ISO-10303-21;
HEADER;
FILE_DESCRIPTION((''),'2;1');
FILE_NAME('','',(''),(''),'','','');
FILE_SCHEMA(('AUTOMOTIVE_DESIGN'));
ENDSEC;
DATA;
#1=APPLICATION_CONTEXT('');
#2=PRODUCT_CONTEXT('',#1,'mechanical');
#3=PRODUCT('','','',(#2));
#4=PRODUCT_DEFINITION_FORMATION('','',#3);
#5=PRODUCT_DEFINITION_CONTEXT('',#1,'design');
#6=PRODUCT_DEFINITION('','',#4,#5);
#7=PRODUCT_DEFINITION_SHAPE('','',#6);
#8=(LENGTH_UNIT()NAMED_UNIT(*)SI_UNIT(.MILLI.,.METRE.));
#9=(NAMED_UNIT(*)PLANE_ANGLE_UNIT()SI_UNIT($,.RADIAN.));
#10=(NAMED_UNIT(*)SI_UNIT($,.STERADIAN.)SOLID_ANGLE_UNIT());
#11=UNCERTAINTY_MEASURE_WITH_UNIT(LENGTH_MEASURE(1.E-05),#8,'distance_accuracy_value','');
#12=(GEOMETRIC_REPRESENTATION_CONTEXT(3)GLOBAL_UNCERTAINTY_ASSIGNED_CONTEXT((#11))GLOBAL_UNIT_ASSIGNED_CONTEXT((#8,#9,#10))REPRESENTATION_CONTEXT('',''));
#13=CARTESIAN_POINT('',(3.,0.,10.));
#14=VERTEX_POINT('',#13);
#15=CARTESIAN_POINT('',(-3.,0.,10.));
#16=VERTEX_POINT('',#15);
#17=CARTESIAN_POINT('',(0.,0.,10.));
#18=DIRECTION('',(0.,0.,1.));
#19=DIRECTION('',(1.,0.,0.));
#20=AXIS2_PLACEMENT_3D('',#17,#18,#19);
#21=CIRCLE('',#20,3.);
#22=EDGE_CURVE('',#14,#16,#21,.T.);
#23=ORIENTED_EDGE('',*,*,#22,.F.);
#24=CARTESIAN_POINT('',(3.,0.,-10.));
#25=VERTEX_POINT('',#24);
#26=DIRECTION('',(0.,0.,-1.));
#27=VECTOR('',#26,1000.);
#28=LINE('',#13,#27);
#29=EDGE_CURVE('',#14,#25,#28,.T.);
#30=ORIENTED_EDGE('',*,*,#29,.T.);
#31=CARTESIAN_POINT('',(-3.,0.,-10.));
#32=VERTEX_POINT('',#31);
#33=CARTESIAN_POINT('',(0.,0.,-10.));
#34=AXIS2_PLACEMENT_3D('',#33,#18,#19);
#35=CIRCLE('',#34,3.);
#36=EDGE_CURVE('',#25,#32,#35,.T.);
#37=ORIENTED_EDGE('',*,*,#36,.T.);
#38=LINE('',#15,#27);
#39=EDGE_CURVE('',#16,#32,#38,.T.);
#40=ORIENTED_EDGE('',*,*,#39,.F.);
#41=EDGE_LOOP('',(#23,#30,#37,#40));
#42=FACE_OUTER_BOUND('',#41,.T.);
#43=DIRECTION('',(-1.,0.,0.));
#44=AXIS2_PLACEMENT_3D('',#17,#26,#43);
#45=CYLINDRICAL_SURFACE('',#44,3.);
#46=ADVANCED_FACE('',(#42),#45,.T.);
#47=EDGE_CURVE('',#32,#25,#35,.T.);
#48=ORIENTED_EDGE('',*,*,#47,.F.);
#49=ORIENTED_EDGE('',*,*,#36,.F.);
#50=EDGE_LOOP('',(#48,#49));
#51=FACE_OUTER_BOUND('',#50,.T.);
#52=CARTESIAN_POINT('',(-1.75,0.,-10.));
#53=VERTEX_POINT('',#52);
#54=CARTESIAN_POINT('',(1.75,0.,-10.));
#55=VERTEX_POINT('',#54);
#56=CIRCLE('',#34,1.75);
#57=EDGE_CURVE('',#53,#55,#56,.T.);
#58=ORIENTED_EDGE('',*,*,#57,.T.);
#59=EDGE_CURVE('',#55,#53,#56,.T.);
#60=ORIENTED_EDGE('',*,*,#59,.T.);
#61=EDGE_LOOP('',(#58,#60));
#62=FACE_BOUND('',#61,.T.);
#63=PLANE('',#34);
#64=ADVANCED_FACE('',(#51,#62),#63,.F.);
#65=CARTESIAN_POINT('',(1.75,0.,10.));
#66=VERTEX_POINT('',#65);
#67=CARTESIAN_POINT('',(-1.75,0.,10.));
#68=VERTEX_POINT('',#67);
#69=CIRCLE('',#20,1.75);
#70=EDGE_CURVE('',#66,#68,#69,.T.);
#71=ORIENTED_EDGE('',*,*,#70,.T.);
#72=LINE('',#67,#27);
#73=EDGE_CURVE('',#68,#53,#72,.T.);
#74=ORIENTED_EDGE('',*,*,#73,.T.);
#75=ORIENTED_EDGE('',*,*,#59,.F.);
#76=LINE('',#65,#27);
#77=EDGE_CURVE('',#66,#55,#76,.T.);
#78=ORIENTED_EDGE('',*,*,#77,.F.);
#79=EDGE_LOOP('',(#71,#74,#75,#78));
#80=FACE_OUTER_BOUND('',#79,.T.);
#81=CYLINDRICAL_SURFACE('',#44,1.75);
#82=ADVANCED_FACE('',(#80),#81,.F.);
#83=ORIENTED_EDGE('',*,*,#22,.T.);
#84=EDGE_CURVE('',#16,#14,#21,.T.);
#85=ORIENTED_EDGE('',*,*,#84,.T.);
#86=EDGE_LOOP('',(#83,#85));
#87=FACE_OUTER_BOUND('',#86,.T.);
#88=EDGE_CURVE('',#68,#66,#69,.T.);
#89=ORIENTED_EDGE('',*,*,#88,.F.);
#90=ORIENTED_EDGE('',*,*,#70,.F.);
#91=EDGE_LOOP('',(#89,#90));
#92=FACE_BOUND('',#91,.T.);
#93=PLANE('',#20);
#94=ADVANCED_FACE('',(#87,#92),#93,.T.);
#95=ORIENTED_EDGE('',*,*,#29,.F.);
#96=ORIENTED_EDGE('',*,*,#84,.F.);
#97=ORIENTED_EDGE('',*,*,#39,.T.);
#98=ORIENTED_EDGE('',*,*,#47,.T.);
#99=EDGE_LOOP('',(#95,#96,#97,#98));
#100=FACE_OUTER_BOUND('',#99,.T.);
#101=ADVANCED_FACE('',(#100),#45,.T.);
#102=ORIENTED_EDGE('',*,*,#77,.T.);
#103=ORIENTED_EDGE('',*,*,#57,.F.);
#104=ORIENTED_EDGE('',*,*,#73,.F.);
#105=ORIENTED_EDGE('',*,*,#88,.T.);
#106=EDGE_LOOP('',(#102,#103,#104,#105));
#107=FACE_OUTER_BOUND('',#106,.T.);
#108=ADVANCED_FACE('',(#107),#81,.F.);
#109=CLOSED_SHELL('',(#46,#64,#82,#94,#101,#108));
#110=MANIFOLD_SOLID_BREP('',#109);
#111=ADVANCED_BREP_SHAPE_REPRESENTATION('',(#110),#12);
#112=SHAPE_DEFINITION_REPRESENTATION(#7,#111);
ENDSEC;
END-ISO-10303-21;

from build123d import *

# Parameters (mm, degrees)
BUSHING_PROFILE_6X_3_5_R   = 3
BUSHING_PROFILE_6X_3_5_R_2 = 1.75
BUSHING_BODY_L20_DEPTH     = 10


with BuildPart() as part:
    # Bushing Profile Ø6xØ3.5 → Bushing Body L20 (new, symmetric)
    with BuildSketch(Plane.XY):
        Circle(BUSHING_PROFILE_6X_3_5_R)
        Circle(BUSHING_PROFILE_6X_3_5_R_2, mode=Mode.SUBTRACT)
    extrude(amount=BUSHING_BODY_L20_DEPTH, both=True)


solid = part.part
